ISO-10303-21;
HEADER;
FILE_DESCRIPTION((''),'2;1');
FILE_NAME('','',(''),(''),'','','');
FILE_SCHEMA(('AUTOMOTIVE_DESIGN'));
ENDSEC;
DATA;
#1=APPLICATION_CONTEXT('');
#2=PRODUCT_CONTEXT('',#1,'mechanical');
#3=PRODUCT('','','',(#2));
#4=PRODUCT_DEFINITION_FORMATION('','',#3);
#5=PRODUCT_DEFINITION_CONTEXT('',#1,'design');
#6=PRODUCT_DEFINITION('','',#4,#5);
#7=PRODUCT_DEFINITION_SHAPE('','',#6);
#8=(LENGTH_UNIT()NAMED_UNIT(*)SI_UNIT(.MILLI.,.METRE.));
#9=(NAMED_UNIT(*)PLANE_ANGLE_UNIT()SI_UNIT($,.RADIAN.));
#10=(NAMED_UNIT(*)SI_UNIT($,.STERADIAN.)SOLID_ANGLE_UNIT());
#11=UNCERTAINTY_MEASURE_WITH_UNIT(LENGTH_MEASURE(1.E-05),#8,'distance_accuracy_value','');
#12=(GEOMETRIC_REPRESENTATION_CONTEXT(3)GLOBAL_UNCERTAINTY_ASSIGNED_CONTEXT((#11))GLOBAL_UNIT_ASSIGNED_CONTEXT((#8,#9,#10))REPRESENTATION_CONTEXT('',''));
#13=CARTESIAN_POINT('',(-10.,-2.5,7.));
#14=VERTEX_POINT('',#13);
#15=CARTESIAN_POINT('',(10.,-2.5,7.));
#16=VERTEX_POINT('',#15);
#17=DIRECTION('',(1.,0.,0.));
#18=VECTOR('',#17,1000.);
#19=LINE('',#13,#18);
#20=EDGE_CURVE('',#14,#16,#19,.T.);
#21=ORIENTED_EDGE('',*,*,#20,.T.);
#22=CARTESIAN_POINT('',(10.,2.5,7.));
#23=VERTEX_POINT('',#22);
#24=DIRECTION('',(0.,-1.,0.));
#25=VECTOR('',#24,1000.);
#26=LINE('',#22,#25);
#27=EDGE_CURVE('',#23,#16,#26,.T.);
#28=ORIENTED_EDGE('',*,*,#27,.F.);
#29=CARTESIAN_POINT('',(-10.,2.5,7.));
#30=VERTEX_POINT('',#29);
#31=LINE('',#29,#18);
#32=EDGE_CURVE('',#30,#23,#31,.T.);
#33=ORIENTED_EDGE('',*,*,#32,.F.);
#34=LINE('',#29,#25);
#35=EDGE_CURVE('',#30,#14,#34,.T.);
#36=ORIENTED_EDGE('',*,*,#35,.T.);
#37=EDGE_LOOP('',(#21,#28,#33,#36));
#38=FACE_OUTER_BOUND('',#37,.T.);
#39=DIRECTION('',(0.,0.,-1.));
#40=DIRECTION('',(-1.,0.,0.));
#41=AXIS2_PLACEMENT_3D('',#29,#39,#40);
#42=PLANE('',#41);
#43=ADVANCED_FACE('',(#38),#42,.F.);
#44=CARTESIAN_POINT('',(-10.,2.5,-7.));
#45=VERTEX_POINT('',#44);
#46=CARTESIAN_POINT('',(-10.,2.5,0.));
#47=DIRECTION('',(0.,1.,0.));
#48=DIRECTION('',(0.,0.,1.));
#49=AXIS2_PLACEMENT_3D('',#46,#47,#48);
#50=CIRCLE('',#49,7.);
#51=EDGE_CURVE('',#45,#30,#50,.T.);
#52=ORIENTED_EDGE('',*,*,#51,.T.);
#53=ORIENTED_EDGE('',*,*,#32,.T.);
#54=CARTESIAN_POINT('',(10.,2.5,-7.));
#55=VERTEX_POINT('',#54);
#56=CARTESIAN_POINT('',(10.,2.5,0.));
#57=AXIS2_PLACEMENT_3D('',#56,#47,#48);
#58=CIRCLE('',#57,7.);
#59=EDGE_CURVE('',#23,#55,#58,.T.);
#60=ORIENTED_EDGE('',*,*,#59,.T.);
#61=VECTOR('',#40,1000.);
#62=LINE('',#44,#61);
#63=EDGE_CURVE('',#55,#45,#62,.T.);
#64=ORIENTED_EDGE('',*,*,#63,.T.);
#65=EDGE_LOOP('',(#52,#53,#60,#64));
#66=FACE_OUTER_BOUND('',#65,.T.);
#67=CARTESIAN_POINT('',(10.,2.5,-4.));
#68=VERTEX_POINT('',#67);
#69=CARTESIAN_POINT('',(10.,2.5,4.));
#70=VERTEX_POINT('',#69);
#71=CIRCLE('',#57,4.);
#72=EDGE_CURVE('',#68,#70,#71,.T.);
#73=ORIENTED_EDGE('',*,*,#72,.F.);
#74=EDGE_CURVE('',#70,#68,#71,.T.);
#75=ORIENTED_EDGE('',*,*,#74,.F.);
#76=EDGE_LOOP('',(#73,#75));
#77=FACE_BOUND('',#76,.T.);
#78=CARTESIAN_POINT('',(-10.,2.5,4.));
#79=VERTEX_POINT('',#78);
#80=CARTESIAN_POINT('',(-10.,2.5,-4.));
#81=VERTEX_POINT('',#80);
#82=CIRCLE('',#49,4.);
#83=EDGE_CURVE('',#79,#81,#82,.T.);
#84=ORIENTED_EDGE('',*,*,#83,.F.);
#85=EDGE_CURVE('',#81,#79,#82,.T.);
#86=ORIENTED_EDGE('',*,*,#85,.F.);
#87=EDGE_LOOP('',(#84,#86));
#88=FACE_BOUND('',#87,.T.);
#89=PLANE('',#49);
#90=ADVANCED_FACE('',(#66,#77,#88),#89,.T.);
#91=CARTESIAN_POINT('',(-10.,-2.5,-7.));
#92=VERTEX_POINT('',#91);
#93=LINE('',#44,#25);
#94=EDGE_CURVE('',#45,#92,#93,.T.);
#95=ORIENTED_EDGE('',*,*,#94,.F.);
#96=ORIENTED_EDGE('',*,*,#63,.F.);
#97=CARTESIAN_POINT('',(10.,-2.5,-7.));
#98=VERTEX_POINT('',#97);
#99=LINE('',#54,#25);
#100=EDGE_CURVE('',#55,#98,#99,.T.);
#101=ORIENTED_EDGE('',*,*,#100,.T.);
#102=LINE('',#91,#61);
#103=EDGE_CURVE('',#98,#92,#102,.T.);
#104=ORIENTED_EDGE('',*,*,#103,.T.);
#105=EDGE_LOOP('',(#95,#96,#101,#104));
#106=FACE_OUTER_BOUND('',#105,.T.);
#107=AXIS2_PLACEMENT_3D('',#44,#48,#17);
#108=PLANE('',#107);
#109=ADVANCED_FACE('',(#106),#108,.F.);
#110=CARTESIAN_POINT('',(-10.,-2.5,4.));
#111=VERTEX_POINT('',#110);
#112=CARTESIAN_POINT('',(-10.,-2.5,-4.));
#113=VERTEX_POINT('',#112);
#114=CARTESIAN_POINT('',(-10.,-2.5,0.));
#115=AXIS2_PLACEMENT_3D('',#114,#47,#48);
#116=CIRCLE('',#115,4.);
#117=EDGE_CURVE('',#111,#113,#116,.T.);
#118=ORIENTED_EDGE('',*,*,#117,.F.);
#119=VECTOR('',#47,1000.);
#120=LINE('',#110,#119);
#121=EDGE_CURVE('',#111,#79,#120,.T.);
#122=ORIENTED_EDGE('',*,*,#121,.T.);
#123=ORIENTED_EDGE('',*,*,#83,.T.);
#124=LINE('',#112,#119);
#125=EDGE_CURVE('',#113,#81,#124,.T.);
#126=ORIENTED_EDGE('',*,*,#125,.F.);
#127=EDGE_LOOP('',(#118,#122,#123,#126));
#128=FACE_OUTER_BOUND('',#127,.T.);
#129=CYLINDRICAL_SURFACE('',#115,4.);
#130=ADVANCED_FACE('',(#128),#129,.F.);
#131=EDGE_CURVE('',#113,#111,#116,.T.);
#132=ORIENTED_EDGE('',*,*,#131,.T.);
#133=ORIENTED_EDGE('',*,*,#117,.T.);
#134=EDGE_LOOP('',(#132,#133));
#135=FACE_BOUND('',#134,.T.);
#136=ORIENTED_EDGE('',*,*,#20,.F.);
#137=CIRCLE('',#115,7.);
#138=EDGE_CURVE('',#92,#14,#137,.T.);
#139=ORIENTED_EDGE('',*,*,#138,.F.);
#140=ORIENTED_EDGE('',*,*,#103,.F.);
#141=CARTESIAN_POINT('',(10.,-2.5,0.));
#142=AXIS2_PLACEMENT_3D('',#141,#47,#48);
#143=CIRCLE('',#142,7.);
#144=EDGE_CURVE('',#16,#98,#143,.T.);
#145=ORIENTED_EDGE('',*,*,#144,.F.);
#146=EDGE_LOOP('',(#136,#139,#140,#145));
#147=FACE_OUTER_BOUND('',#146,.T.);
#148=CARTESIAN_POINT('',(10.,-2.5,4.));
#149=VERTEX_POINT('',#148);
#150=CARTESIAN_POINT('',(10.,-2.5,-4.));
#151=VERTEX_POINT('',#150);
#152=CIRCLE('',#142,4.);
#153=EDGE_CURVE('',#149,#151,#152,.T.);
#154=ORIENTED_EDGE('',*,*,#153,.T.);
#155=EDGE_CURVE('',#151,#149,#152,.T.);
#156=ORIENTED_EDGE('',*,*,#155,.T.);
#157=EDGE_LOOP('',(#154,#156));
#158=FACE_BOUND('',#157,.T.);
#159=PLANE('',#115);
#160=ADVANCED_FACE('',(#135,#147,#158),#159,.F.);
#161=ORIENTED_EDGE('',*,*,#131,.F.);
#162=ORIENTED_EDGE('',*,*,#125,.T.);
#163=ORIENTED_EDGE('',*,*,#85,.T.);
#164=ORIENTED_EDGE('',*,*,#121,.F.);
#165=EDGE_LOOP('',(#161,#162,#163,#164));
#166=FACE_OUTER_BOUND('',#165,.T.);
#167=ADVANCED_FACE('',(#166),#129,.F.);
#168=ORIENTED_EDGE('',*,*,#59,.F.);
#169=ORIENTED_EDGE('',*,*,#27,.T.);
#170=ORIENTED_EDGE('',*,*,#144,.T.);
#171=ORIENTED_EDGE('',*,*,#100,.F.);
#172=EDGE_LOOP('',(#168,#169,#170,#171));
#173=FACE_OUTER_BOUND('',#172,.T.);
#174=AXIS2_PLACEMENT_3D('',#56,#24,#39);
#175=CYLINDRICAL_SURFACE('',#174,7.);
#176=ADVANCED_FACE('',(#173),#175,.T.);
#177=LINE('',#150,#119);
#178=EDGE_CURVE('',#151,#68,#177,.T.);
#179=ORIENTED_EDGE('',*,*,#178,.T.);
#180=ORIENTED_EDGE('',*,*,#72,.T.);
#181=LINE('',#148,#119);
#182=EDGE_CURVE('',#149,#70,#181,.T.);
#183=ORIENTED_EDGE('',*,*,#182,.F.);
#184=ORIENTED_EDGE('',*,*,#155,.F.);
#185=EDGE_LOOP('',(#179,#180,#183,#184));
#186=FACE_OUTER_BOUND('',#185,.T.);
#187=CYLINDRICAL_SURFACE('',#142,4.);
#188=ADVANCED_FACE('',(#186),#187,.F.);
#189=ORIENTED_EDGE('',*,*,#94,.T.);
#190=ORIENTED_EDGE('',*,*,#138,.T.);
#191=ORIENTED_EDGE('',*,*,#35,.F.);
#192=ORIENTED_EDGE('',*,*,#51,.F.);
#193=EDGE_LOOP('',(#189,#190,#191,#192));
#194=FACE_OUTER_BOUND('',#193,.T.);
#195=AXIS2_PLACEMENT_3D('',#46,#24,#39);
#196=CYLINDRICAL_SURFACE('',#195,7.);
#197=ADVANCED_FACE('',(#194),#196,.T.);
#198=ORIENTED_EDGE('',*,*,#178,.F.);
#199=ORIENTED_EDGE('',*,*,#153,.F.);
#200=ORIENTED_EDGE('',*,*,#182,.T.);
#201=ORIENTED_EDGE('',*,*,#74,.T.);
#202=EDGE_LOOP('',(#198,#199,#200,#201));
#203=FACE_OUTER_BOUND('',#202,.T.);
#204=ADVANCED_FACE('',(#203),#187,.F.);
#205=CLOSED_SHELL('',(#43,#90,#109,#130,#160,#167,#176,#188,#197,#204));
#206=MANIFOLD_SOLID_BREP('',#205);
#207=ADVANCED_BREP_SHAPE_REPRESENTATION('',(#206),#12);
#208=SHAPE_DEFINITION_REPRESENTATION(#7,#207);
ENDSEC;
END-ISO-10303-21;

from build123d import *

# Parameters (mm, degrees)
LINK_PLATE_DEPTH         = 2.5
HOLE_SKETCH_R            = 4
THROUGH_HOLES_2X_8_DEPTH = 2.5


with BuildPart() as part:
    # Link Profile Sketch → Link Plate (new, symmetric)
    with BuildSketch(Plane(origin=(0, 0, 0), x_dir=(1, 0, 0), z_dir=(0, 1, 0))):
        with BuildLine():
            Line((-10, 7), (10, 7))
            ThreePointArc((10, 7), (17, 0), (10, -7))
            Line((10, -7), (-10, -7))
            ThreePointArc((-10, -7), (-17, 0), (-10, 7))
        make_face()
    extrude(amount=LINK_PLATE_DEPTH, both=True)

    # Hole Sketch → Through Holes 2xØ8 (cut, symmetric)
    with BuildSketch(Plane(origin=(0, 0, 0), x_dir=(1, 0, 0), z_dir=(0, 1, 0))):
        with Locations(Location((10, 0, 0), (0, 0, 270))):
            Circle(HOLE_SKETCH_R)
        with Locations(Location((-10, 0, 0), (0, 0, 270))):
            Circle(HOLE_SKETCH_R)
    extrude(amount=THROUGH_HOLES_2X_8_DEPTH, both=True, mode=Mode.SUBTRACT)


solid = part.part
